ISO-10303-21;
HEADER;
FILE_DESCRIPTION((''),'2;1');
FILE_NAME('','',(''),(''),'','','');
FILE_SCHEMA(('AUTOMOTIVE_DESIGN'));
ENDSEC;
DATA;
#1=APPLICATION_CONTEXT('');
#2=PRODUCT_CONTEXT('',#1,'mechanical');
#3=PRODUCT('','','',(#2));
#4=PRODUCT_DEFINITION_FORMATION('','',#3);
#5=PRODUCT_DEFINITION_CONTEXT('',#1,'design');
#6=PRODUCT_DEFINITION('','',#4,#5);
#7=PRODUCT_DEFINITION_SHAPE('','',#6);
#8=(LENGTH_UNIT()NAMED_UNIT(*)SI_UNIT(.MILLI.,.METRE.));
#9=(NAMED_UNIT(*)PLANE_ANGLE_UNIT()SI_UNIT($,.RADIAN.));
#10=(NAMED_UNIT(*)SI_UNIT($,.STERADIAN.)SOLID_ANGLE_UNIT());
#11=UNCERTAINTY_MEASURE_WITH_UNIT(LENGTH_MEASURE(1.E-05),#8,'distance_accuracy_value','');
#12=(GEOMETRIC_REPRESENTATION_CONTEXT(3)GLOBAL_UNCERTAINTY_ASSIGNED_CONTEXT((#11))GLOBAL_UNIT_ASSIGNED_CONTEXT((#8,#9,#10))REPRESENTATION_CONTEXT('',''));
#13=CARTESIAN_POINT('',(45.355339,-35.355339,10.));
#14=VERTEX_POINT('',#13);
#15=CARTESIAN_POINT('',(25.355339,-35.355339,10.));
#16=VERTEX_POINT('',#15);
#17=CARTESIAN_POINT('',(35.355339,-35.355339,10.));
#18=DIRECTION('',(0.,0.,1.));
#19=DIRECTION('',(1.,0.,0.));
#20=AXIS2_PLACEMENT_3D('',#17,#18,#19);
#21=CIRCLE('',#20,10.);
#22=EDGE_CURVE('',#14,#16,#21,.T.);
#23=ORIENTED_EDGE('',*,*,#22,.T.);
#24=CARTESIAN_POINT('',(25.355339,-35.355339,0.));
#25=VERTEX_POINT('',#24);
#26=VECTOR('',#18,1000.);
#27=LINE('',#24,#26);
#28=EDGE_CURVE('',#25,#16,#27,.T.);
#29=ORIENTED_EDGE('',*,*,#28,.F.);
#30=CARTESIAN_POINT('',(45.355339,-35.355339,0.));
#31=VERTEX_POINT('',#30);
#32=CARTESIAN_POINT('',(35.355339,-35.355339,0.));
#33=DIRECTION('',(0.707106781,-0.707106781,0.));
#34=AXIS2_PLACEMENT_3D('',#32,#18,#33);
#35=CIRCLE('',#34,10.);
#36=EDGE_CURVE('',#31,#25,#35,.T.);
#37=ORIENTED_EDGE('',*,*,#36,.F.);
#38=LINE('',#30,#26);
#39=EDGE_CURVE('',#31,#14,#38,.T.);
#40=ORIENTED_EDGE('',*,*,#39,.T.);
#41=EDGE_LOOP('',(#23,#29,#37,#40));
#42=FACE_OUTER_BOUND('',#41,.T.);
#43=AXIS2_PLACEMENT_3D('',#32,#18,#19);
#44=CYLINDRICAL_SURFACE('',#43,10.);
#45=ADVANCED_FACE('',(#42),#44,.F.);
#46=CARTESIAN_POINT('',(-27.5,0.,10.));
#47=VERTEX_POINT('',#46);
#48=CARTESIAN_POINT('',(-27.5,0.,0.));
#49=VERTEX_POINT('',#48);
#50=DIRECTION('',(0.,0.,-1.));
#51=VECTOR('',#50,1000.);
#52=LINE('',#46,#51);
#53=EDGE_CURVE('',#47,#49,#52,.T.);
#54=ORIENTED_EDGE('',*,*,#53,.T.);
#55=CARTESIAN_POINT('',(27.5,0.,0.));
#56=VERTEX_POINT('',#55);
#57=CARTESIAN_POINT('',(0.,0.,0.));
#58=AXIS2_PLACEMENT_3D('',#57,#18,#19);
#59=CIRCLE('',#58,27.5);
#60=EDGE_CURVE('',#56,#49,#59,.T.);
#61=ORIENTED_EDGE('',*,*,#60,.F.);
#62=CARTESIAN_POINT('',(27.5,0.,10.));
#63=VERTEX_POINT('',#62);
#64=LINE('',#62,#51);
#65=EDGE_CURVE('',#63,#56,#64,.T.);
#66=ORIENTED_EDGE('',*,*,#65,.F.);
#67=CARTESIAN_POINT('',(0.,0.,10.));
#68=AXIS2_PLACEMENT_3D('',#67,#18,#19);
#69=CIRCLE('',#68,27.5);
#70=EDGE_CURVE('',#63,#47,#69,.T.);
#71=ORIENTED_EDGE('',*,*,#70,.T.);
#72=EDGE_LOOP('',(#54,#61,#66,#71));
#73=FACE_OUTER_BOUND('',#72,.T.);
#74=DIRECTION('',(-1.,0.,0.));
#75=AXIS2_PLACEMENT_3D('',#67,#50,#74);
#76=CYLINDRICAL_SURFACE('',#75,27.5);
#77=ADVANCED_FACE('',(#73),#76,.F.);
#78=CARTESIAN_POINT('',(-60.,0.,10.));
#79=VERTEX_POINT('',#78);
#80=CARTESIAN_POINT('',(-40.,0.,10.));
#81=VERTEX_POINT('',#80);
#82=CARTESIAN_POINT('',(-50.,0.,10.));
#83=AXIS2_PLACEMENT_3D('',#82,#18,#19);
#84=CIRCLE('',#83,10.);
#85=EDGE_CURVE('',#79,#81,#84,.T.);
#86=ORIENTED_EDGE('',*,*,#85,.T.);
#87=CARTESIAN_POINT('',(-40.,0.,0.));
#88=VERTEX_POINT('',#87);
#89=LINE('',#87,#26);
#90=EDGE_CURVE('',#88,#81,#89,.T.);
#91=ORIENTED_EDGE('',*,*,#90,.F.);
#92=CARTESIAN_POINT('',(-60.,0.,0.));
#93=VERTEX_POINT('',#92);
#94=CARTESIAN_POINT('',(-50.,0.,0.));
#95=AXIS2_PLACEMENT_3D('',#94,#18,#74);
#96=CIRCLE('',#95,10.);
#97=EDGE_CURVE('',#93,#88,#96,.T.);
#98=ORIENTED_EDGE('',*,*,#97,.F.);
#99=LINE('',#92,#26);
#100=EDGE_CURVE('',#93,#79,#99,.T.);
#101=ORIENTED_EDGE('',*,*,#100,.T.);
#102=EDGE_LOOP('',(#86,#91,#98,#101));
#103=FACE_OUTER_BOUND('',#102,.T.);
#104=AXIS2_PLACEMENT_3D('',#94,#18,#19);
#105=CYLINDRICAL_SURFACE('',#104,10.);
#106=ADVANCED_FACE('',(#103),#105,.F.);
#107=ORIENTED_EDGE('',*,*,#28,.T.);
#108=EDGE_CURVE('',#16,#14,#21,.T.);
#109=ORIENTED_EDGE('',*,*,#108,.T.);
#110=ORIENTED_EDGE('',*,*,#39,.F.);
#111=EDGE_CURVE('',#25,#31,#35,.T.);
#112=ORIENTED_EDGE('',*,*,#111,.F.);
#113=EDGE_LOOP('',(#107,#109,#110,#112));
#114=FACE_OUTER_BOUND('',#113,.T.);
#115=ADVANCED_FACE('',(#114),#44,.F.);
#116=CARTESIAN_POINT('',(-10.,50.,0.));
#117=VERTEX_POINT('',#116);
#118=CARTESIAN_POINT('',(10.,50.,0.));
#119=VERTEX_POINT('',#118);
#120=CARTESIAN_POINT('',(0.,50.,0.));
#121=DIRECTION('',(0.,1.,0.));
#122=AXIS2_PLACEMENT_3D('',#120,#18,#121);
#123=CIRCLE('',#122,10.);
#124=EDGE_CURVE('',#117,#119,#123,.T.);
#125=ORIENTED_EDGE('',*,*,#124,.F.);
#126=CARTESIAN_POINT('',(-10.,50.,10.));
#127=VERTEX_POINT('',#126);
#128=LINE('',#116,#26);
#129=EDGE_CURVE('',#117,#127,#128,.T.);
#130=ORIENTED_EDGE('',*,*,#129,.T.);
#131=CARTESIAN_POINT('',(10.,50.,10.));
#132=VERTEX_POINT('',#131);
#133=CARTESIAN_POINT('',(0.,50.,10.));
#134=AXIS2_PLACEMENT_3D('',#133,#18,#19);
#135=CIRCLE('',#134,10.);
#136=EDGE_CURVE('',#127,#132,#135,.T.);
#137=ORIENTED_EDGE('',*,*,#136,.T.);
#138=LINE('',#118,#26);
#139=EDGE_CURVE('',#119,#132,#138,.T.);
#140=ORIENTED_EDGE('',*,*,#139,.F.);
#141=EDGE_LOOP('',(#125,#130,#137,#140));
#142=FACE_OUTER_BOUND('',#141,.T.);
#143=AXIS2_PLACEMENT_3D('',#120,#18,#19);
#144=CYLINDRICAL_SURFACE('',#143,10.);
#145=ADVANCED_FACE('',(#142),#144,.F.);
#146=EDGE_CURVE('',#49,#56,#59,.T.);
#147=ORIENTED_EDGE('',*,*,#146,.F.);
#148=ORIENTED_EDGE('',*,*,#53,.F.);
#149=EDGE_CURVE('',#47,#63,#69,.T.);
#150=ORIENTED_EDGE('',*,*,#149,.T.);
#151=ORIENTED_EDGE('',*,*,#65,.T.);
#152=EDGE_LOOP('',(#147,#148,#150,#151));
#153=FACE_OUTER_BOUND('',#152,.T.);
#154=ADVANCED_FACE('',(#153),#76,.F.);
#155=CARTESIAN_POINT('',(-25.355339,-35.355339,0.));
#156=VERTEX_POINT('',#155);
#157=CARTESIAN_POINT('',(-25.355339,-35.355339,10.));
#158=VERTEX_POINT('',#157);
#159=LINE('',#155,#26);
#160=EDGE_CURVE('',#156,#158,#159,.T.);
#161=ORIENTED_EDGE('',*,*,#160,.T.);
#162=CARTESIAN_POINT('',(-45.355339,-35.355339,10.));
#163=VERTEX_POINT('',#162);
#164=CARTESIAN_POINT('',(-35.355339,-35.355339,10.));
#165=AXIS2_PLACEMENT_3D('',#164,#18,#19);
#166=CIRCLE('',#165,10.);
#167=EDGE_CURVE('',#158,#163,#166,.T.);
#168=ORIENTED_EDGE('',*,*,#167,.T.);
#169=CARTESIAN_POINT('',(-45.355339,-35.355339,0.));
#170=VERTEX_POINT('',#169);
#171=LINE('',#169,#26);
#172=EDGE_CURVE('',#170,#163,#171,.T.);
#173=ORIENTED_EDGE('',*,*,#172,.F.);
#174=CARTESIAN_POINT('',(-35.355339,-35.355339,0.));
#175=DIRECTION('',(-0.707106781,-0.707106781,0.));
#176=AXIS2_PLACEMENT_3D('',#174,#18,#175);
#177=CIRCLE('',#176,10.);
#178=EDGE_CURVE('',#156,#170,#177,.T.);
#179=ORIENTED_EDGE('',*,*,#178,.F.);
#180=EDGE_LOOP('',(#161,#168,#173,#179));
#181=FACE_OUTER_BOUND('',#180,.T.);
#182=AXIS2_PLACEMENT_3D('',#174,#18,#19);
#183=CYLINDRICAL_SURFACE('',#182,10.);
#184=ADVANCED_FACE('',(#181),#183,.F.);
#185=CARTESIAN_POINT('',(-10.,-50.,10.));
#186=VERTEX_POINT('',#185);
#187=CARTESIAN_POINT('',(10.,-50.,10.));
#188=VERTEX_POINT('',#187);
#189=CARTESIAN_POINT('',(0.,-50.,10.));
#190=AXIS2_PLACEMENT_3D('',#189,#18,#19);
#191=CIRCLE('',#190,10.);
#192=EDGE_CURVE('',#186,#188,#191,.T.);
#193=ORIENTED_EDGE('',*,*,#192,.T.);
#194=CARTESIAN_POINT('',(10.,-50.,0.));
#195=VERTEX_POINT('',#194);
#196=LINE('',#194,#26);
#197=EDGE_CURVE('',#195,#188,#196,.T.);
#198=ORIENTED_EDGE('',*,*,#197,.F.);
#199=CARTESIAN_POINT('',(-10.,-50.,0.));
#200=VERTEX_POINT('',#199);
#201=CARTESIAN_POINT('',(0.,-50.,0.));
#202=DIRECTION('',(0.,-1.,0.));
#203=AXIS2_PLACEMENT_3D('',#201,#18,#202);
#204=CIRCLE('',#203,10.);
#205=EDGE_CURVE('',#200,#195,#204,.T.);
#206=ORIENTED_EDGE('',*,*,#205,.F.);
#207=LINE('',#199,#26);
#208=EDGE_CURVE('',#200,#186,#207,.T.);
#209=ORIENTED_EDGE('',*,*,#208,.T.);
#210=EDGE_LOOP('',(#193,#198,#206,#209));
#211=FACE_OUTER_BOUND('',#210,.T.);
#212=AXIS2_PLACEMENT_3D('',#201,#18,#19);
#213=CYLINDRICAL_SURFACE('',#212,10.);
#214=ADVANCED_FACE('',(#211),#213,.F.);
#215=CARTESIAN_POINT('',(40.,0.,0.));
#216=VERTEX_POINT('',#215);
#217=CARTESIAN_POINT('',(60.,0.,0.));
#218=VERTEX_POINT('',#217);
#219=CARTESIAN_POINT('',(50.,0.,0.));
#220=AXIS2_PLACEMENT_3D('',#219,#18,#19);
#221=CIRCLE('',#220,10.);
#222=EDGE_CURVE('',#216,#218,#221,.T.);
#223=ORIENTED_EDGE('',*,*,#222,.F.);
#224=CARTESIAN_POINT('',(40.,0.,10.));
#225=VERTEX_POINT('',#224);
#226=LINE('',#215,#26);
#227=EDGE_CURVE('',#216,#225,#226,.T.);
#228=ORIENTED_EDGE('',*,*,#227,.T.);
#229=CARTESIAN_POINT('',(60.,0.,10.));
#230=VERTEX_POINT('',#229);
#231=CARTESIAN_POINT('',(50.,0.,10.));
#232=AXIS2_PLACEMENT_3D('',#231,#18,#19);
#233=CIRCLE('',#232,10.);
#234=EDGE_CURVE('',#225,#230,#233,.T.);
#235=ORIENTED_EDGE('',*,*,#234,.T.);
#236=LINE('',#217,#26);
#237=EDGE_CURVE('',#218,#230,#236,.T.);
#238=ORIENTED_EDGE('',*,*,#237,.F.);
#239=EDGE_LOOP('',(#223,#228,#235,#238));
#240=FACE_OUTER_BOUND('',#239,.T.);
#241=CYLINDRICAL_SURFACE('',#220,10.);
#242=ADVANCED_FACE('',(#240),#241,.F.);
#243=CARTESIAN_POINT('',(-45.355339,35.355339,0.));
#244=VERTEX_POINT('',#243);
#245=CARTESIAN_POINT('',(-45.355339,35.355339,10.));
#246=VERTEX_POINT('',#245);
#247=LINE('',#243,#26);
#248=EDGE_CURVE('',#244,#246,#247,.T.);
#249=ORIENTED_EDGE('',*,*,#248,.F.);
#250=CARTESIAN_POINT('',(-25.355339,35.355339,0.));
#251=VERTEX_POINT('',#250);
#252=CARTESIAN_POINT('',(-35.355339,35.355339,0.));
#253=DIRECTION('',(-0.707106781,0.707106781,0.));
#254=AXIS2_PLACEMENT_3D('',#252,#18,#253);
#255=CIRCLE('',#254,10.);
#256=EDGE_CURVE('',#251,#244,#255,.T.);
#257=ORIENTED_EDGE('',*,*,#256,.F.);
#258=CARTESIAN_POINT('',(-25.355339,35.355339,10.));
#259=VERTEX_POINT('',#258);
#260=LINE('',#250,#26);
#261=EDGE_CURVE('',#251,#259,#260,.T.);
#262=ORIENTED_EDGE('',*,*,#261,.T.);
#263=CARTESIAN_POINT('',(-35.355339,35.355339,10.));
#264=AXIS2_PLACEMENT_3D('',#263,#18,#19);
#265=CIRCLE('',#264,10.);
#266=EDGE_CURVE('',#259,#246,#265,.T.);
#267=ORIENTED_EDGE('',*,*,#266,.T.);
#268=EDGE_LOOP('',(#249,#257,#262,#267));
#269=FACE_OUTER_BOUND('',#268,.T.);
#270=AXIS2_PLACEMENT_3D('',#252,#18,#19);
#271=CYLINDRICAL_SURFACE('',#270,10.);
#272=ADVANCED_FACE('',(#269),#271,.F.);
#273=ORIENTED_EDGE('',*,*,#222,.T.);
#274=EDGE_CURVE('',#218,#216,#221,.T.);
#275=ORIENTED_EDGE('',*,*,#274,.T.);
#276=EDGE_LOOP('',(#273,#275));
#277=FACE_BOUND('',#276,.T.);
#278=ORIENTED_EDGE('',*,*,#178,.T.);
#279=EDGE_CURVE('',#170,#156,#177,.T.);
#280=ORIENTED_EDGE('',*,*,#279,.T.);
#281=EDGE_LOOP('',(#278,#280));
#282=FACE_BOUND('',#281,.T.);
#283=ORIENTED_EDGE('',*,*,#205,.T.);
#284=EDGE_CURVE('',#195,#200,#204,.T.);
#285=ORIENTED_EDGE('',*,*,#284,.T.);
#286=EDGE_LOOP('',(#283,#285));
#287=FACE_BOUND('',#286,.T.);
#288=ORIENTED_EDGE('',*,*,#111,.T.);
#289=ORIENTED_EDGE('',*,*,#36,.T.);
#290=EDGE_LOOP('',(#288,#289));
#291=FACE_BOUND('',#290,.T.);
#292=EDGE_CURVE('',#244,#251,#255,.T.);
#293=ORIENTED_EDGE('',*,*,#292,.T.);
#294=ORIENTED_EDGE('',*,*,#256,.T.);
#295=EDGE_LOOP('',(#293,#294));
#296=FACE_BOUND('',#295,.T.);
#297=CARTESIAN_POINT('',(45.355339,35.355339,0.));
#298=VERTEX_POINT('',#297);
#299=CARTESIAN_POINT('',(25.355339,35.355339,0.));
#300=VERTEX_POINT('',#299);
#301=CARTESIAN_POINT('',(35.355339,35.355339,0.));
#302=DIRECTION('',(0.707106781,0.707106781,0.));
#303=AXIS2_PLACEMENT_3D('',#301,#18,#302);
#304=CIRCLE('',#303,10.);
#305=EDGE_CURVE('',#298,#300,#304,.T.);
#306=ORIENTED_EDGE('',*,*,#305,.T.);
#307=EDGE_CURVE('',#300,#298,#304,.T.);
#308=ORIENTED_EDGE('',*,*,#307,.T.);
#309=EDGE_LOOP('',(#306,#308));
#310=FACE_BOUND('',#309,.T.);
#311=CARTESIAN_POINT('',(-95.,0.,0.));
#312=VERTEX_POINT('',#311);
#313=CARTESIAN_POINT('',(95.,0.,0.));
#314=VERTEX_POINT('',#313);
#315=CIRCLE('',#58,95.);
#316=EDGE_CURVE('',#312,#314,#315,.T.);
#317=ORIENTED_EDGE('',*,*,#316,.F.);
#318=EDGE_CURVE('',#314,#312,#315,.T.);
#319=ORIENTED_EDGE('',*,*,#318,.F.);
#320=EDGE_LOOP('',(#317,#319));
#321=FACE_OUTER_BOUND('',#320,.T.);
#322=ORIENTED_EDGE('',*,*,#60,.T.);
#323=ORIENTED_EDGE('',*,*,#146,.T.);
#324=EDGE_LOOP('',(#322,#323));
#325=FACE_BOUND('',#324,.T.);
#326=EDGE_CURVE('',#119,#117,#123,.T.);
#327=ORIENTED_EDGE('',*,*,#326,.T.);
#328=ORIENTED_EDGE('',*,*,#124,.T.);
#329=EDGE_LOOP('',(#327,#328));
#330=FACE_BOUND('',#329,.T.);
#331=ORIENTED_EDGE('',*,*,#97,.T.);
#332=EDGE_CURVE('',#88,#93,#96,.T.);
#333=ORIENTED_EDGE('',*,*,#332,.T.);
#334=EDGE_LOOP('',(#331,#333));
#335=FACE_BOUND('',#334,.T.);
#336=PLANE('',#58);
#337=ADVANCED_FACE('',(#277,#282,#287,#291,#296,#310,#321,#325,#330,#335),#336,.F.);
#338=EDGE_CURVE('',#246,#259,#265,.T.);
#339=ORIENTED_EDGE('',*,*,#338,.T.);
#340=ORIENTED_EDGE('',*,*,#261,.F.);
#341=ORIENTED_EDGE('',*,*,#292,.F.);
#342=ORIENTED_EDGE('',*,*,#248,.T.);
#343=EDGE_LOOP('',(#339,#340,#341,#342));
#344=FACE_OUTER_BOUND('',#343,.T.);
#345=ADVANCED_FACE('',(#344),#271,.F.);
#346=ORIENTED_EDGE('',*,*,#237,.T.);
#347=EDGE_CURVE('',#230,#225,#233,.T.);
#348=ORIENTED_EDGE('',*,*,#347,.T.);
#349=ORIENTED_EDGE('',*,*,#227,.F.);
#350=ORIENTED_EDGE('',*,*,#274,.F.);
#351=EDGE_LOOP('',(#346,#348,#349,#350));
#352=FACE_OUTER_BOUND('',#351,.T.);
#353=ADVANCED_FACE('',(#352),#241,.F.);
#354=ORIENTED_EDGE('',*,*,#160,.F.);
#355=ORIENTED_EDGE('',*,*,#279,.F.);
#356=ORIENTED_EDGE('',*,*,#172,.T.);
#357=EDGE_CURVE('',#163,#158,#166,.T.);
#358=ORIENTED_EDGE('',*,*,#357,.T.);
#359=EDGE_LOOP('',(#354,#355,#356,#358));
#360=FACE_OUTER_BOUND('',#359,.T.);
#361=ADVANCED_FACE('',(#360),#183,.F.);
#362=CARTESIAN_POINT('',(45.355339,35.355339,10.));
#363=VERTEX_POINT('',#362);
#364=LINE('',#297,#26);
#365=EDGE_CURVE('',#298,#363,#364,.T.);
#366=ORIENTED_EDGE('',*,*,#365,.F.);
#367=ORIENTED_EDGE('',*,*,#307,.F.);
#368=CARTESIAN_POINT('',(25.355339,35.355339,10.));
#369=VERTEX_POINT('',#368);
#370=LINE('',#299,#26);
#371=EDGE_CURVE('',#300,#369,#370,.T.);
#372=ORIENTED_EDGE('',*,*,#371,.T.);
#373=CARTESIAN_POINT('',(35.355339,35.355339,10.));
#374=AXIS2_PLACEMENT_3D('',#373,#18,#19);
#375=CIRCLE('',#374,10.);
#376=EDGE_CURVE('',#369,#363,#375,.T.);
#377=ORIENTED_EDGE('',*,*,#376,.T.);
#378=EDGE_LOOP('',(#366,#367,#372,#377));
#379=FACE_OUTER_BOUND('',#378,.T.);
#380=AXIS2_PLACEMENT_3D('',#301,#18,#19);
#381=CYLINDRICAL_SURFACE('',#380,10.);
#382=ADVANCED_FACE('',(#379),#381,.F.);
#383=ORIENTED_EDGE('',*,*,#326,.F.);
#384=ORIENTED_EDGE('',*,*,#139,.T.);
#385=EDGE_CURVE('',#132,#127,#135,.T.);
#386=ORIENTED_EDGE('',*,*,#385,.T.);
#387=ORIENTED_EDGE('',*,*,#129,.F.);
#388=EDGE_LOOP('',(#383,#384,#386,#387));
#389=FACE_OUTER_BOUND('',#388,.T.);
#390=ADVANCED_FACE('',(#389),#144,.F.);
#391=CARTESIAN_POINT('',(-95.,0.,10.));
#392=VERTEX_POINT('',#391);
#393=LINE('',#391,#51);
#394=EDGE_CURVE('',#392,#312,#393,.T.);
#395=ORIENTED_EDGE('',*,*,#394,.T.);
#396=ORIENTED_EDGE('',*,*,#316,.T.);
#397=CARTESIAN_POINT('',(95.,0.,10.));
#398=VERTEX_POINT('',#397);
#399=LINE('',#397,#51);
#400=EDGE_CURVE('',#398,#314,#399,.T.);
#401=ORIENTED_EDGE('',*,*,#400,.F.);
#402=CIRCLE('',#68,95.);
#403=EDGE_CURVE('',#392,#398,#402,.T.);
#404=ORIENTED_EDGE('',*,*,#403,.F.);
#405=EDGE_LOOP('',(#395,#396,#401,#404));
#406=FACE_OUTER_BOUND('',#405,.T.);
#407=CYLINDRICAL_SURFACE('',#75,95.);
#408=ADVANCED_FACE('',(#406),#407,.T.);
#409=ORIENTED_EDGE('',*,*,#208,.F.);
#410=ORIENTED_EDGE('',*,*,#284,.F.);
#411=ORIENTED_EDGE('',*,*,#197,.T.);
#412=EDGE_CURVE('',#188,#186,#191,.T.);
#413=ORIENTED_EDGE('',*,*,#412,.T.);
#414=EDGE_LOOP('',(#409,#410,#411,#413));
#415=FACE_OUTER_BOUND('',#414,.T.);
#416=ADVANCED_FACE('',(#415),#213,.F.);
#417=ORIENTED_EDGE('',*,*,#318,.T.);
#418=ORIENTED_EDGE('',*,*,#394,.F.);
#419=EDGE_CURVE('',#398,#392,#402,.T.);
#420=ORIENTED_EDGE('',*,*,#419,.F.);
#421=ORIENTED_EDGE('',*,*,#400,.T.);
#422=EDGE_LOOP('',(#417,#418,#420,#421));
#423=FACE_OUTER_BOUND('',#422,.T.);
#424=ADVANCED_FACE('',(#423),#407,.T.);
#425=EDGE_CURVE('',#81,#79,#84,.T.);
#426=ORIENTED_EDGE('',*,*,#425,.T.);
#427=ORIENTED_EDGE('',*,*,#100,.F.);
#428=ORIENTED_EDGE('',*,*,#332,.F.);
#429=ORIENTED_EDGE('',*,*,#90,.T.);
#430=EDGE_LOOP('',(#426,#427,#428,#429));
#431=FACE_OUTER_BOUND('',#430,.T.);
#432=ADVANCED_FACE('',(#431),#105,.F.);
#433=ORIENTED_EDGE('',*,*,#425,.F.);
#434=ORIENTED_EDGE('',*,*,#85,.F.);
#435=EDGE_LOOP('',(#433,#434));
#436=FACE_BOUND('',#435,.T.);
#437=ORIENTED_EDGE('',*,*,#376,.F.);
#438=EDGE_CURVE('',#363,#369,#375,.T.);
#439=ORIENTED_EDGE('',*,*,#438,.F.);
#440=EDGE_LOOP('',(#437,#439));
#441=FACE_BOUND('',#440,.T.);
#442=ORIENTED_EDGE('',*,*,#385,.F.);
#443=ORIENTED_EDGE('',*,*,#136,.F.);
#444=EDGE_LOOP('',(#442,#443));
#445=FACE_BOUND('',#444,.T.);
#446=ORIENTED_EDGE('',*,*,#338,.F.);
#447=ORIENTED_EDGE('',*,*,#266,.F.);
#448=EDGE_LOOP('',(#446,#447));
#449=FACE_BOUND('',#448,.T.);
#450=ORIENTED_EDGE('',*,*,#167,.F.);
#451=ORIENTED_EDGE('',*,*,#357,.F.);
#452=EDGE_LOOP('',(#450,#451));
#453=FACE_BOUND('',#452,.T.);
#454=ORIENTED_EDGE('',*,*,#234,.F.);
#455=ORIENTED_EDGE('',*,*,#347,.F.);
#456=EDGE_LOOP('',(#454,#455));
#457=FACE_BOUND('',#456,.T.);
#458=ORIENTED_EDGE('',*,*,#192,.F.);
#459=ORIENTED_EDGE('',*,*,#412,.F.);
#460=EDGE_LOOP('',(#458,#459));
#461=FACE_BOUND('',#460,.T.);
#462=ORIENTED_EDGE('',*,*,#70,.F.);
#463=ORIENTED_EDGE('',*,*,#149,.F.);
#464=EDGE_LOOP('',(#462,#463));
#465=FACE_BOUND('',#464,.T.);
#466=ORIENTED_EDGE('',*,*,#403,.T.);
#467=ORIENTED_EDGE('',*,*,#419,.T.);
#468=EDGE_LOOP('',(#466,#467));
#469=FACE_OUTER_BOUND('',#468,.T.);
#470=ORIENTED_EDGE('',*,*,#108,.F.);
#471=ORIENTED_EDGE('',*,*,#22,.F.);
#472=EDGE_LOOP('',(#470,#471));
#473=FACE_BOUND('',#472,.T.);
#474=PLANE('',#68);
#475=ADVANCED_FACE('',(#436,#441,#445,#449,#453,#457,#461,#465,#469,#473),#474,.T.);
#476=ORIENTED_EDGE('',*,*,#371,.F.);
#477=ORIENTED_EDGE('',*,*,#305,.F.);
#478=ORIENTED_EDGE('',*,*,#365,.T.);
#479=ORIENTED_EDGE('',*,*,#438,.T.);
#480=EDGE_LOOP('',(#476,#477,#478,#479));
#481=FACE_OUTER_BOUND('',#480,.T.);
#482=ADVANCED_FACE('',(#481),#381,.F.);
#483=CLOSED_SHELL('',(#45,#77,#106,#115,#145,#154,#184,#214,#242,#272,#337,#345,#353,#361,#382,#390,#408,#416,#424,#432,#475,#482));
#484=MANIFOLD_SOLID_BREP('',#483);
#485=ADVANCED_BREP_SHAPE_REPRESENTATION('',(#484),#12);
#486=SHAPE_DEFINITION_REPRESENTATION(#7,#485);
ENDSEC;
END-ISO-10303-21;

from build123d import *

# Parameters (mm, degrees)
SKETCH2_R           = 95
SKETCH2_R_2         = 27.5
BOSS_EXTRUDE1_DEPTH = 10
SKETCH3_R           = 10
CUT_EXTRUDE1_DEPTH  = 135.721935853
CIRPATTERN1_COUNT   = 8


with BuildPart() as part:
    # Sketch2 → Boss-Extrude1 (new body)
    with BuildSketch(Plane.XY):
        Circle(SKETCH2_R)
        Circle(SKETCH2_R_2, mode=Mode.SUBTRACT)
    extrude(amount=BOSS_EXTRUDE1_DEPTH)

    # Sketch3 → Cut-Extrude1 (cut, symmetric)
    with BuildSketch(Plane.XY.offset(10)):
        with Locations((50, 0)):
            Circle(SKETCH3_R)
    cut_extrude1 = extrude(amount=CUT_EXTRUDE1_DEPTH, both=True, mode=Mode.SUBTRACT)

    # CirPattern1: Cut-Extrude1 ×8 about axis
    cirpattern1_axis = Axis((0, 0, 0), (0, 0, 1))
    for i in range(1, CIRPATTERN1_COUNT):
        add(cut_extrude1.rotate(cirpattern1_axis, i * 360 / CIRPATTERN1_COUNT), mode=Mode.SUBTRACT)


solid = part.part
